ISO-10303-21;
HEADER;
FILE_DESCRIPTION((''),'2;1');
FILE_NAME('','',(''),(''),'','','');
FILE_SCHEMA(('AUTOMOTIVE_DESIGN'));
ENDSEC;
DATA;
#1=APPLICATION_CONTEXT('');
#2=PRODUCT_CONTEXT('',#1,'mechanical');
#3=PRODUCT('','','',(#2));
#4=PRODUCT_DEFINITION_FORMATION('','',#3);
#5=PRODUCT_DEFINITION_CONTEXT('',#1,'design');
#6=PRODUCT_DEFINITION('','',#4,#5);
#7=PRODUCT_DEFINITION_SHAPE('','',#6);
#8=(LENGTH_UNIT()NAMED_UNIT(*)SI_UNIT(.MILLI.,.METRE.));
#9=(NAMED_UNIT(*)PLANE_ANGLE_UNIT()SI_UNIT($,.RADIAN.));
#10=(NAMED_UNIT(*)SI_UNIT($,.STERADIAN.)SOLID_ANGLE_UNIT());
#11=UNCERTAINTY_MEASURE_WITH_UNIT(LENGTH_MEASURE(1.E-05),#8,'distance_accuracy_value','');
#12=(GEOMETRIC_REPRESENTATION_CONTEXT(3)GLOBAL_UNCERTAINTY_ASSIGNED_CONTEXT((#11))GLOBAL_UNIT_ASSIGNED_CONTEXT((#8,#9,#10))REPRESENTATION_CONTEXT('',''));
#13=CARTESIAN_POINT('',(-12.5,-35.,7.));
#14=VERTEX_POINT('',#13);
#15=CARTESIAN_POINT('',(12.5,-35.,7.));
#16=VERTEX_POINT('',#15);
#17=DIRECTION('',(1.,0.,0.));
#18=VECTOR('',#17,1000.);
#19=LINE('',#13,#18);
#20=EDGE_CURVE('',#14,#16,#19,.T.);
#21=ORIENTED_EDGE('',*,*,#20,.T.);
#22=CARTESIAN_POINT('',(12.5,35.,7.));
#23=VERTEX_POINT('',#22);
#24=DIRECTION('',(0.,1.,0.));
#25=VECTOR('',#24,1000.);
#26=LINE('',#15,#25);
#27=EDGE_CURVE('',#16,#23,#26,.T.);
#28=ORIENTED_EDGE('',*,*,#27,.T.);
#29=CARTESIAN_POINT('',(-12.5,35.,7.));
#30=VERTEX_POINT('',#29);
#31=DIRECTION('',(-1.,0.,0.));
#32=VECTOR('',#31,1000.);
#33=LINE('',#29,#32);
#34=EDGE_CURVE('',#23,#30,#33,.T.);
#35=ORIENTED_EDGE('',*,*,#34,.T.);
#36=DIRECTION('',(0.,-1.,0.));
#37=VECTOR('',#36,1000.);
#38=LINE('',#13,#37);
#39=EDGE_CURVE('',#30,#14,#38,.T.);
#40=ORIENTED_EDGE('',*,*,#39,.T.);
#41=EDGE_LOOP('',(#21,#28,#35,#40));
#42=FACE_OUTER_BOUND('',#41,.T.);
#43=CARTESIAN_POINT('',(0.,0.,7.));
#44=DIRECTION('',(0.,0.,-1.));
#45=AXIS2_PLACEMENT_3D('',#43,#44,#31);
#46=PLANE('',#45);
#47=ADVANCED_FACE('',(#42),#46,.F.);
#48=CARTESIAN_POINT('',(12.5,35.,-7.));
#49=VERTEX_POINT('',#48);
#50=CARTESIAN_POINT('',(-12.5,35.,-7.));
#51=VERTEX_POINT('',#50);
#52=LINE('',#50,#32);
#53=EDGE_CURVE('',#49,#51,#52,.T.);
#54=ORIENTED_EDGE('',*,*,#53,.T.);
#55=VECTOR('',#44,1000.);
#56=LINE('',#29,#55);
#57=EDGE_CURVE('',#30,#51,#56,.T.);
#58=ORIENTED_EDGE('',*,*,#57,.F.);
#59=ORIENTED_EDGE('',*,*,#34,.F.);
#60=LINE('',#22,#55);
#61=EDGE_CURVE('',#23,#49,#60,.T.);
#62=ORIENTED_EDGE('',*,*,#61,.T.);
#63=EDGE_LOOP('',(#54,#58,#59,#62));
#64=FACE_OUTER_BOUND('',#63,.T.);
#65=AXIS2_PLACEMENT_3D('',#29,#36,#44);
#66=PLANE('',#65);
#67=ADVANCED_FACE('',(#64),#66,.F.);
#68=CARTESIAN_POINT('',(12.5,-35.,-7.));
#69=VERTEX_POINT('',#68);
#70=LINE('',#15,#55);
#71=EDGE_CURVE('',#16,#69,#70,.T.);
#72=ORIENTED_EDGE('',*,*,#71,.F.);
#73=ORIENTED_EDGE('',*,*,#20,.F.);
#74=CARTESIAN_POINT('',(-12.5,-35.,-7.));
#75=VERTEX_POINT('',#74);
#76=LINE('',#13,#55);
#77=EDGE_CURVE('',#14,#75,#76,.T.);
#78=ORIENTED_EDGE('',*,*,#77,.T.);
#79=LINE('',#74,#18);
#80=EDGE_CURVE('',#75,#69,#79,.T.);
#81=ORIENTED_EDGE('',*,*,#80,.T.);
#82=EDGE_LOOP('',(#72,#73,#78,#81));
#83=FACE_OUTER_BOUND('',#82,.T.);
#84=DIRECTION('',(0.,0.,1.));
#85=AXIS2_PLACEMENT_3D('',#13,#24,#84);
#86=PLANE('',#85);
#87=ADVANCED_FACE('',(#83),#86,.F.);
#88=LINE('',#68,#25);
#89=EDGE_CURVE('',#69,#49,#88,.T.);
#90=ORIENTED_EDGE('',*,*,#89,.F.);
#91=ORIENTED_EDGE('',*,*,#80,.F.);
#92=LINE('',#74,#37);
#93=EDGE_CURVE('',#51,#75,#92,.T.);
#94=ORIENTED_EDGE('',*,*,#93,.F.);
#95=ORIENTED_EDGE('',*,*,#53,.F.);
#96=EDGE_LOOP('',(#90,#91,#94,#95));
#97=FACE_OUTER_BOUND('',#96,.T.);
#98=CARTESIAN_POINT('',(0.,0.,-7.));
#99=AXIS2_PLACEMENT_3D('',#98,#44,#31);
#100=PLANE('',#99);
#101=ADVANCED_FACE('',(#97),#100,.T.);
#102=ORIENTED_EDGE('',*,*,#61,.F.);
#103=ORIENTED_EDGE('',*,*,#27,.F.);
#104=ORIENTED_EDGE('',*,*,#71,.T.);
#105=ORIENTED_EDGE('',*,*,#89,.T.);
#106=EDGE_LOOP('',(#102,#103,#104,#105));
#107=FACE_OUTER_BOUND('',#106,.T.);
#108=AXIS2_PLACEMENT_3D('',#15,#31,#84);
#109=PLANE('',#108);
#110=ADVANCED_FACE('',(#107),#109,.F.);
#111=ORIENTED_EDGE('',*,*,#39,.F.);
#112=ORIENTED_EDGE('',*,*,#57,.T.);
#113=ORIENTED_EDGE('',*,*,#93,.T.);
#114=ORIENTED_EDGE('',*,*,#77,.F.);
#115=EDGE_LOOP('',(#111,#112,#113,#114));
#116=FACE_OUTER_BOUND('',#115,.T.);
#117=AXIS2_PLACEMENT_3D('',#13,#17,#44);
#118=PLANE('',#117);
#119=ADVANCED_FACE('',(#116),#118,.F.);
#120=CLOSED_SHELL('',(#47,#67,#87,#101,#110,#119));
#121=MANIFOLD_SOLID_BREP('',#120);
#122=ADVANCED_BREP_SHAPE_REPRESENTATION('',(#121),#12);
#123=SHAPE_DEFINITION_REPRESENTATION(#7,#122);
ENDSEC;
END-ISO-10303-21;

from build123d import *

# Parameters (mm, degrees)
SKETCH_1_W      = 25
SKETCH_1_H      = 70
EXTRUDE_1_DEPTH = 7


with BuildPart() as part:
    # 草图1 → 凸台-拉伸1 (new, symmetric)
    with BuildSketch(Plane.XY):
        Rectangle(SKETCH_1_W, SKETCH_1_H)
    extrude(amount=EXTRUDE_1_DEPTH, both=True)


solid = part.part
